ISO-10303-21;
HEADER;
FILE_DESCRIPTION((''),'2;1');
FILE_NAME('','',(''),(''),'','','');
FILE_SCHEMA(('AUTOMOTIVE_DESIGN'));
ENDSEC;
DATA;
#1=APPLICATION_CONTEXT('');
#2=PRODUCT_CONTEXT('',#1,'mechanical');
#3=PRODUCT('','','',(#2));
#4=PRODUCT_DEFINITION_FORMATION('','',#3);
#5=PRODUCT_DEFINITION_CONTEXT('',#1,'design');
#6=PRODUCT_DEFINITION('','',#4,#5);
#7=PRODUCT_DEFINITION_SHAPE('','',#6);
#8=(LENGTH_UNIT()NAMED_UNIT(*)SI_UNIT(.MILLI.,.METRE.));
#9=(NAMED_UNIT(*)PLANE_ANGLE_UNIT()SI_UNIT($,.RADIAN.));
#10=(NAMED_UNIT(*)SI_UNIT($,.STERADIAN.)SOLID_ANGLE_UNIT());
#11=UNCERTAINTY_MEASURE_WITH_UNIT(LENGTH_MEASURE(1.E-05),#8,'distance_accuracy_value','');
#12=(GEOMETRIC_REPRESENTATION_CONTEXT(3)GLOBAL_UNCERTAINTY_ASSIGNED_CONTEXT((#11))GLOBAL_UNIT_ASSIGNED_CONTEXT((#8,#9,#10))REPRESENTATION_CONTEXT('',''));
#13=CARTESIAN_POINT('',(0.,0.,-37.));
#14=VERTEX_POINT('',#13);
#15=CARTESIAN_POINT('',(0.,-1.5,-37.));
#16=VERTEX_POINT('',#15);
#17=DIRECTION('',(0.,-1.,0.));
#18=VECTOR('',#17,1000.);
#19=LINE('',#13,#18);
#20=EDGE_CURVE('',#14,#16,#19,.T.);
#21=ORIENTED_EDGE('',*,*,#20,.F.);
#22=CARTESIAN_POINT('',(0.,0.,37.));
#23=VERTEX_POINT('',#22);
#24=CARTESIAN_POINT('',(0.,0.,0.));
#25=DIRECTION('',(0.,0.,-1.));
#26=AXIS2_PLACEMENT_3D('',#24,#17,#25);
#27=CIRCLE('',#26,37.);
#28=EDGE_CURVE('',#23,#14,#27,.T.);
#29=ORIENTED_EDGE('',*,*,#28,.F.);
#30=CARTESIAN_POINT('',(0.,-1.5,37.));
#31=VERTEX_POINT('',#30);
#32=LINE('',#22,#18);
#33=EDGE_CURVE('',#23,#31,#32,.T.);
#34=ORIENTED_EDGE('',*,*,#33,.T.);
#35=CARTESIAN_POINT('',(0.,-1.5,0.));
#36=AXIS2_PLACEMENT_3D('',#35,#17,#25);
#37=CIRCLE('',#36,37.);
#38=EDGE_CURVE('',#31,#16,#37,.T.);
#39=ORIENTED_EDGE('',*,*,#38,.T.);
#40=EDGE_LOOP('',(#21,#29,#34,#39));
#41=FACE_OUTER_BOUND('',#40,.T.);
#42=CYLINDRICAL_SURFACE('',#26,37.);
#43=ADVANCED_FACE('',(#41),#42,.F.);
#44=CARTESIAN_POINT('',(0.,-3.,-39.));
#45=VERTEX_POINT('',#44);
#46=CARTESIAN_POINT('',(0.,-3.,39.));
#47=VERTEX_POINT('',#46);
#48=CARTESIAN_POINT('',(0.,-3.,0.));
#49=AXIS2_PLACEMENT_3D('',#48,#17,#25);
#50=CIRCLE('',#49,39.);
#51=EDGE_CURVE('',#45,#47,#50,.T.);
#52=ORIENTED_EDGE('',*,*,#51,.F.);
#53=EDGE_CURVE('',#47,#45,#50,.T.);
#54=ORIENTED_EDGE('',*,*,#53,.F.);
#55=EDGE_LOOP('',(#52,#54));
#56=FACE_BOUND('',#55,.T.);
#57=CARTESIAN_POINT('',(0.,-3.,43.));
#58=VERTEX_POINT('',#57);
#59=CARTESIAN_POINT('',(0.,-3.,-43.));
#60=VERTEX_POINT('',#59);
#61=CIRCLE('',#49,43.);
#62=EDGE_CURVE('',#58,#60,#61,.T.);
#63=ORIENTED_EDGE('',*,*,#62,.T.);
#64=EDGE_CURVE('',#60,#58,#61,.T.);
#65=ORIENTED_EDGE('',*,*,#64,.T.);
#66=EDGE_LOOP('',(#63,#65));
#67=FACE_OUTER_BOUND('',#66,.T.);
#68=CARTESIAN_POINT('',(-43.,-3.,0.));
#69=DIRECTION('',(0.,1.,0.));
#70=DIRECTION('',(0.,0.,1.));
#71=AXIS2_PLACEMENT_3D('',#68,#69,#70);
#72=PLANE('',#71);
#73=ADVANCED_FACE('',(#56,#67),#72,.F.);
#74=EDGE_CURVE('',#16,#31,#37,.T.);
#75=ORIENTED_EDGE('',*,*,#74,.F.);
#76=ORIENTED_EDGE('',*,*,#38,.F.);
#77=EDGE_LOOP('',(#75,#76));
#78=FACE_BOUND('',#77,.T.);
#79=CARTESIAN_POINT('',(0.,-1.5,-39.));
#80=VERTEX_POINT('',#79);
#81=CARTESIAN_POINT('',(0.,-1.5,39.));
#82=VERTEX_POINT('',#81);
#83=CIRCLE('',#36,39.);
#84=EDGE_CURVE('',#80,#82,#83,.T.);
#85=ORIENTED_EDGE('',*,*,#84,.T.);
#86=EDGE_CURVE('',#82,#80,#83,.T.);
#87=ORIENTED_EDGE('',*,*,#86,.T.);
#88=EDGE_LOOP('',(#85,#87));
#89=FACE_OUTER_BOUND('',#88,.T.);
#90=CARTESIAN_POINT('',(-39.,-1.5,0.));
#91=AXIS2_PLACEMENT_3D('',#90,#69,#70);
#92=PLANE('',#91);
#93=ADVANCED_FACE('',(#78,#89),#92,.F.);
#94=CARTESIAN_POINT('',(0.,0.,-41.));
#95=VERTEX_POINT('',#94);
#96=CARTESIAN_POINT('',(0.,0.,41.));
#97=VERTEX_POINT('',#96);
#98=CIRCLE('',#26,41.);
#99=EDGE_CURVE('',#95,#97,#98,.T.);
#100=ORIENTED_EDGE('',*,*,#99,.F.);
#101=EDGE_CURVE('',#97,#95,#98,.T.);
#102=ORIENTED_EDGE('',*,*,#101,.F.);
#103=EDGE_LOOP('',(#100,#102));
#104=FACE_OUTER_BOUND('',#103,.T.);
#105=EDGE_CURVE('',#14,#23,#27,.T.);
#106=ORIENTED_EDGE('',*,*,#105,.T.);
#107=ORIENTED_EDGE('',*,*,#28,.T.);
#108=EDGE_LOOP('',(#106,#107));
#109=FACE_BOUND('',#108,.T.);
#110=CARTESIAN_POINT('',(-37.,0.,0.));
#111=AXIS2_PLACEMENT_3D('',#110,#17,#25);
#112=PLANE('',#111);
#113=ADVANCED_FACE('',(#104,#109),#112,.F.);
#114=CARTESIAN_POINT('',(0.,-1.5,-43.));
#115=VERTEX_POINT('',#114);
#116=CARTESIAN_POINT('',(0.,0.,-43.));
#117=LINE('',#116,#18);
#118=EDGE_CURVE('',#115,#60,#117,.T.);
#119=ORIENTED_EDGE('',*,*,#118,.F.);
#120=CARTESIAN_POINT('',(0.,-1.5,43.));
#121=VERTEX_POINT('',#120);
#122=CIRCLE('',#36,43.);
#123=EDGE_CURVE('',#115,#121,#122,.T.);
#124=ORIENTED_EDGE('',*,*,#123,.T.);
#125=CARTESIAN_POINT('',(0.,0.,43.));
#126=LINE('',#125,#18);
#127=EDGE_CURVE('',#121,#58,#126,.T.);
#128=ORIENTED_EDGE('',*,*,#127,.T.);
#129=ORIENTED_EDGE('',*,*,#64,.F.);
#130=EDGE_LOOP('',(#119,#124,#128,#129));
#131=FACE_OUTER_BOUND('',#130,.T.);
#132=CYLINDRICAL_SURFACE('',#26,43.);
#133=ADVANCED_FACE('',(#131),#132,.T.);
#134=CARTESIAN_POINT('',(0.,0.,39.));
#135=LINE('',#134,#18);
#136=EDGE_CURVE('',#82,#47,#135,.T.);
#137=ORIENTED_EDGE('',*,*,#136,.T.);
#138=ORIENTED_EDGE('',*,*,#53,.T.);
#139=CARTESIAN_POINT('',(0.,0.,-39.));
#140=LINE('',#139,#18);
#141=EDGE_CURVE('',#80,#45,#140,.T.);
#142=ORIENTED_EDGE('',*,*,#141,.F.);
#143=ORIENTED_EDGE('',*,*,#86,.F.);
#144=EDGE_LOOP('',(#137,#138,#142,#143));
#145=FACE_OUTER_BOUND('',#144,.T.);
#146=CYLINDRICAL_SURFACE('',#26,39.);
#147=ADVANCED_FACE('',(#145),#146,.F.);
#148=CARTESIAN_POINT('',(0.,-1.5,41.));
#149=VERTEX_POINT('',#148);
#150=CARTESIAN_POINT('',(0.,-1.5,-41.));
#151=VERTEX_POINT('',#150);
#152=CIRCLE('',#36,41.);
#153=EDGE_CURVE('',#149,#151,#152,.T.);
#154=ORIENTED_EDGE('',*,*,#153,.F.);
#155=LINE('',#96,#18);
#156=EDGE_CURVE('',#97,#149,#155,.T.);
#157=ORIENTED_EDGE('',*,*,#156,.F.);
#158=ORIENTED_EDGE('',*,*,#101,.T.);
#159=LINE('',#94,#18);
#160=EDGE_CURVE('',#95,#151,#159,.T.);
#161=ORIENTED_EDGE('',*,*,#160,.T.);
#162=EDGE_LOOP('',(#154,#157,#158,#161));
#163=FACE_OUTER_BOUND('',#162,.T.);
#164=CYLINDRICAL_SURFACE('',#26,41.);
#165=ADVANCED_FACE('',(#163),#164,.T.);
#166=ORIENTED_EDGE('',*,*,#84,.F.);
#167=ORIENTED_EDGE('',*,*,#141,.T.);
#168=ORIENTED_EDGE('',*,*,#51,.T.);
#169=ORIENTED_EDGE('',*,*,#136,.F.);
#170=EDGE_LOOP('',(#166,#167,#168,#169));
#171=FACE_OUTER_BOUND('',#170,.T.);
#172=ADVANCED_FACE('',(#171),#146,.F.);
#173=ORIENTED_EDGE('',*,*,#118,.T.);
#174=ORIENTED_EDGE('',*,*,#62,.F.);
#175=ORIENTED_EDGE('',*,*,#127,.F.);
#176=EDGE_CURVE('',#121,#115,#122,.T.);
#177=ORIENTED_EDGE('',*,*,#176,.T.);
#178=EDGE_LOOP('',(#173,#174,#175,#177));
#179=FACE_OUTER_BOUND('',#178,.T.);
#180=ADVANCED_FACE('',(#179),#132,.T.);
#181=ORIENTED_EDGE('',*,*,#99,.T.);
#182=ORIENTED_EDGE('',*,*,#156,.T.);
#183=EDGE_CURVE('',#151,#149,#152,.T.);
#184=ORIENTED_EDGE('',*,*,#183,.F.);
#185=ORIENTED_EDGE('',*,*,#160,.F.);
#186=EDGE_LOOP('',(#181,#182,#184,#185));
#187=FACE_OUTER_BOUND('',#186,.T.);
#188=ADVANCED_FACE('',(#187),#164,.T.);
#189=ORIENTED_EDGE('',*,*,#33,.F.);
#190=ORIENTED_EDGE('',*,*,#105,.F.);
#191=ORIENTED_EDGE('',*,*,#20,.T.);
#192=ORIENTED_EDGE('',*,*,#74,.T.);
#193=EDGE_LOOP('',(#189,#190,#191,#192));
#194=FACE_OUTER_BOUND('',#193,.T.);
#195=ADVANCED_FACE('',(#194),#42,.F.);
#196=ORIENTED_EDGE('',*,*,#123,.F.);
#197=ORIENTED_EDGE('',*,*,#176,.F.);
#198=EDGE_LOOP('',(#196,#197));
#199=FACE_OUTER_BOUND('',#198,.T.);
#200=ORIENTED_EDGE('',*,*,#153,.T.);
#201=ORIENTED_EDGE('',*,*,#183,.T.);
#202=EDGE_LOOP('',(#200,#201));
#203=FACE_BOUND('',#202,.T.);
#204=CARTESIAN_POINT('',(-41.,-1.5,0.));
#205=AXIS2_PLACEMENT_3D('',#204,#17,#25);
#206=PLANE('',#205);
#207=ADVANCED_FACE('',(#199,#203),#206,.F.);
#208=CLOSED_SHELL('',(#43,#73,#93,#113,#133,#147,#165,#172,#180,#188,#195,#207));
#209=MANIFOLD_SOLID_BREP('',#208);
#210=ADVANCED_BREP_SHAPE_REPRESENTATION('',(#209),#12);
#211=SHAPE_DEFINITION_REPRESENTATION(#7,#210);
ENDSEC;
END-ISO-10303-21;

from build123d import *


with BuildPart() as part:
    # 草图1 → 旋转1 (revolve)
    with BuildSketch(Plane.XY, mode=Mode.PRIVATE) as revolve_1_sk:
        Polygon((-37, 0), (-41, 0), (-41, -1.5), (-43, -1.5), (-43, -3), (-39, -3), (-39, -1.5), (-37, -1.5), align=None)
    revolve(revolve_1_sk.sketch.rotate(Axis((0, 0, 0), (0, 1, 0)), 270), axis=Axis((0, 0, 0), (0, 1, 0)))


solid = part.part
